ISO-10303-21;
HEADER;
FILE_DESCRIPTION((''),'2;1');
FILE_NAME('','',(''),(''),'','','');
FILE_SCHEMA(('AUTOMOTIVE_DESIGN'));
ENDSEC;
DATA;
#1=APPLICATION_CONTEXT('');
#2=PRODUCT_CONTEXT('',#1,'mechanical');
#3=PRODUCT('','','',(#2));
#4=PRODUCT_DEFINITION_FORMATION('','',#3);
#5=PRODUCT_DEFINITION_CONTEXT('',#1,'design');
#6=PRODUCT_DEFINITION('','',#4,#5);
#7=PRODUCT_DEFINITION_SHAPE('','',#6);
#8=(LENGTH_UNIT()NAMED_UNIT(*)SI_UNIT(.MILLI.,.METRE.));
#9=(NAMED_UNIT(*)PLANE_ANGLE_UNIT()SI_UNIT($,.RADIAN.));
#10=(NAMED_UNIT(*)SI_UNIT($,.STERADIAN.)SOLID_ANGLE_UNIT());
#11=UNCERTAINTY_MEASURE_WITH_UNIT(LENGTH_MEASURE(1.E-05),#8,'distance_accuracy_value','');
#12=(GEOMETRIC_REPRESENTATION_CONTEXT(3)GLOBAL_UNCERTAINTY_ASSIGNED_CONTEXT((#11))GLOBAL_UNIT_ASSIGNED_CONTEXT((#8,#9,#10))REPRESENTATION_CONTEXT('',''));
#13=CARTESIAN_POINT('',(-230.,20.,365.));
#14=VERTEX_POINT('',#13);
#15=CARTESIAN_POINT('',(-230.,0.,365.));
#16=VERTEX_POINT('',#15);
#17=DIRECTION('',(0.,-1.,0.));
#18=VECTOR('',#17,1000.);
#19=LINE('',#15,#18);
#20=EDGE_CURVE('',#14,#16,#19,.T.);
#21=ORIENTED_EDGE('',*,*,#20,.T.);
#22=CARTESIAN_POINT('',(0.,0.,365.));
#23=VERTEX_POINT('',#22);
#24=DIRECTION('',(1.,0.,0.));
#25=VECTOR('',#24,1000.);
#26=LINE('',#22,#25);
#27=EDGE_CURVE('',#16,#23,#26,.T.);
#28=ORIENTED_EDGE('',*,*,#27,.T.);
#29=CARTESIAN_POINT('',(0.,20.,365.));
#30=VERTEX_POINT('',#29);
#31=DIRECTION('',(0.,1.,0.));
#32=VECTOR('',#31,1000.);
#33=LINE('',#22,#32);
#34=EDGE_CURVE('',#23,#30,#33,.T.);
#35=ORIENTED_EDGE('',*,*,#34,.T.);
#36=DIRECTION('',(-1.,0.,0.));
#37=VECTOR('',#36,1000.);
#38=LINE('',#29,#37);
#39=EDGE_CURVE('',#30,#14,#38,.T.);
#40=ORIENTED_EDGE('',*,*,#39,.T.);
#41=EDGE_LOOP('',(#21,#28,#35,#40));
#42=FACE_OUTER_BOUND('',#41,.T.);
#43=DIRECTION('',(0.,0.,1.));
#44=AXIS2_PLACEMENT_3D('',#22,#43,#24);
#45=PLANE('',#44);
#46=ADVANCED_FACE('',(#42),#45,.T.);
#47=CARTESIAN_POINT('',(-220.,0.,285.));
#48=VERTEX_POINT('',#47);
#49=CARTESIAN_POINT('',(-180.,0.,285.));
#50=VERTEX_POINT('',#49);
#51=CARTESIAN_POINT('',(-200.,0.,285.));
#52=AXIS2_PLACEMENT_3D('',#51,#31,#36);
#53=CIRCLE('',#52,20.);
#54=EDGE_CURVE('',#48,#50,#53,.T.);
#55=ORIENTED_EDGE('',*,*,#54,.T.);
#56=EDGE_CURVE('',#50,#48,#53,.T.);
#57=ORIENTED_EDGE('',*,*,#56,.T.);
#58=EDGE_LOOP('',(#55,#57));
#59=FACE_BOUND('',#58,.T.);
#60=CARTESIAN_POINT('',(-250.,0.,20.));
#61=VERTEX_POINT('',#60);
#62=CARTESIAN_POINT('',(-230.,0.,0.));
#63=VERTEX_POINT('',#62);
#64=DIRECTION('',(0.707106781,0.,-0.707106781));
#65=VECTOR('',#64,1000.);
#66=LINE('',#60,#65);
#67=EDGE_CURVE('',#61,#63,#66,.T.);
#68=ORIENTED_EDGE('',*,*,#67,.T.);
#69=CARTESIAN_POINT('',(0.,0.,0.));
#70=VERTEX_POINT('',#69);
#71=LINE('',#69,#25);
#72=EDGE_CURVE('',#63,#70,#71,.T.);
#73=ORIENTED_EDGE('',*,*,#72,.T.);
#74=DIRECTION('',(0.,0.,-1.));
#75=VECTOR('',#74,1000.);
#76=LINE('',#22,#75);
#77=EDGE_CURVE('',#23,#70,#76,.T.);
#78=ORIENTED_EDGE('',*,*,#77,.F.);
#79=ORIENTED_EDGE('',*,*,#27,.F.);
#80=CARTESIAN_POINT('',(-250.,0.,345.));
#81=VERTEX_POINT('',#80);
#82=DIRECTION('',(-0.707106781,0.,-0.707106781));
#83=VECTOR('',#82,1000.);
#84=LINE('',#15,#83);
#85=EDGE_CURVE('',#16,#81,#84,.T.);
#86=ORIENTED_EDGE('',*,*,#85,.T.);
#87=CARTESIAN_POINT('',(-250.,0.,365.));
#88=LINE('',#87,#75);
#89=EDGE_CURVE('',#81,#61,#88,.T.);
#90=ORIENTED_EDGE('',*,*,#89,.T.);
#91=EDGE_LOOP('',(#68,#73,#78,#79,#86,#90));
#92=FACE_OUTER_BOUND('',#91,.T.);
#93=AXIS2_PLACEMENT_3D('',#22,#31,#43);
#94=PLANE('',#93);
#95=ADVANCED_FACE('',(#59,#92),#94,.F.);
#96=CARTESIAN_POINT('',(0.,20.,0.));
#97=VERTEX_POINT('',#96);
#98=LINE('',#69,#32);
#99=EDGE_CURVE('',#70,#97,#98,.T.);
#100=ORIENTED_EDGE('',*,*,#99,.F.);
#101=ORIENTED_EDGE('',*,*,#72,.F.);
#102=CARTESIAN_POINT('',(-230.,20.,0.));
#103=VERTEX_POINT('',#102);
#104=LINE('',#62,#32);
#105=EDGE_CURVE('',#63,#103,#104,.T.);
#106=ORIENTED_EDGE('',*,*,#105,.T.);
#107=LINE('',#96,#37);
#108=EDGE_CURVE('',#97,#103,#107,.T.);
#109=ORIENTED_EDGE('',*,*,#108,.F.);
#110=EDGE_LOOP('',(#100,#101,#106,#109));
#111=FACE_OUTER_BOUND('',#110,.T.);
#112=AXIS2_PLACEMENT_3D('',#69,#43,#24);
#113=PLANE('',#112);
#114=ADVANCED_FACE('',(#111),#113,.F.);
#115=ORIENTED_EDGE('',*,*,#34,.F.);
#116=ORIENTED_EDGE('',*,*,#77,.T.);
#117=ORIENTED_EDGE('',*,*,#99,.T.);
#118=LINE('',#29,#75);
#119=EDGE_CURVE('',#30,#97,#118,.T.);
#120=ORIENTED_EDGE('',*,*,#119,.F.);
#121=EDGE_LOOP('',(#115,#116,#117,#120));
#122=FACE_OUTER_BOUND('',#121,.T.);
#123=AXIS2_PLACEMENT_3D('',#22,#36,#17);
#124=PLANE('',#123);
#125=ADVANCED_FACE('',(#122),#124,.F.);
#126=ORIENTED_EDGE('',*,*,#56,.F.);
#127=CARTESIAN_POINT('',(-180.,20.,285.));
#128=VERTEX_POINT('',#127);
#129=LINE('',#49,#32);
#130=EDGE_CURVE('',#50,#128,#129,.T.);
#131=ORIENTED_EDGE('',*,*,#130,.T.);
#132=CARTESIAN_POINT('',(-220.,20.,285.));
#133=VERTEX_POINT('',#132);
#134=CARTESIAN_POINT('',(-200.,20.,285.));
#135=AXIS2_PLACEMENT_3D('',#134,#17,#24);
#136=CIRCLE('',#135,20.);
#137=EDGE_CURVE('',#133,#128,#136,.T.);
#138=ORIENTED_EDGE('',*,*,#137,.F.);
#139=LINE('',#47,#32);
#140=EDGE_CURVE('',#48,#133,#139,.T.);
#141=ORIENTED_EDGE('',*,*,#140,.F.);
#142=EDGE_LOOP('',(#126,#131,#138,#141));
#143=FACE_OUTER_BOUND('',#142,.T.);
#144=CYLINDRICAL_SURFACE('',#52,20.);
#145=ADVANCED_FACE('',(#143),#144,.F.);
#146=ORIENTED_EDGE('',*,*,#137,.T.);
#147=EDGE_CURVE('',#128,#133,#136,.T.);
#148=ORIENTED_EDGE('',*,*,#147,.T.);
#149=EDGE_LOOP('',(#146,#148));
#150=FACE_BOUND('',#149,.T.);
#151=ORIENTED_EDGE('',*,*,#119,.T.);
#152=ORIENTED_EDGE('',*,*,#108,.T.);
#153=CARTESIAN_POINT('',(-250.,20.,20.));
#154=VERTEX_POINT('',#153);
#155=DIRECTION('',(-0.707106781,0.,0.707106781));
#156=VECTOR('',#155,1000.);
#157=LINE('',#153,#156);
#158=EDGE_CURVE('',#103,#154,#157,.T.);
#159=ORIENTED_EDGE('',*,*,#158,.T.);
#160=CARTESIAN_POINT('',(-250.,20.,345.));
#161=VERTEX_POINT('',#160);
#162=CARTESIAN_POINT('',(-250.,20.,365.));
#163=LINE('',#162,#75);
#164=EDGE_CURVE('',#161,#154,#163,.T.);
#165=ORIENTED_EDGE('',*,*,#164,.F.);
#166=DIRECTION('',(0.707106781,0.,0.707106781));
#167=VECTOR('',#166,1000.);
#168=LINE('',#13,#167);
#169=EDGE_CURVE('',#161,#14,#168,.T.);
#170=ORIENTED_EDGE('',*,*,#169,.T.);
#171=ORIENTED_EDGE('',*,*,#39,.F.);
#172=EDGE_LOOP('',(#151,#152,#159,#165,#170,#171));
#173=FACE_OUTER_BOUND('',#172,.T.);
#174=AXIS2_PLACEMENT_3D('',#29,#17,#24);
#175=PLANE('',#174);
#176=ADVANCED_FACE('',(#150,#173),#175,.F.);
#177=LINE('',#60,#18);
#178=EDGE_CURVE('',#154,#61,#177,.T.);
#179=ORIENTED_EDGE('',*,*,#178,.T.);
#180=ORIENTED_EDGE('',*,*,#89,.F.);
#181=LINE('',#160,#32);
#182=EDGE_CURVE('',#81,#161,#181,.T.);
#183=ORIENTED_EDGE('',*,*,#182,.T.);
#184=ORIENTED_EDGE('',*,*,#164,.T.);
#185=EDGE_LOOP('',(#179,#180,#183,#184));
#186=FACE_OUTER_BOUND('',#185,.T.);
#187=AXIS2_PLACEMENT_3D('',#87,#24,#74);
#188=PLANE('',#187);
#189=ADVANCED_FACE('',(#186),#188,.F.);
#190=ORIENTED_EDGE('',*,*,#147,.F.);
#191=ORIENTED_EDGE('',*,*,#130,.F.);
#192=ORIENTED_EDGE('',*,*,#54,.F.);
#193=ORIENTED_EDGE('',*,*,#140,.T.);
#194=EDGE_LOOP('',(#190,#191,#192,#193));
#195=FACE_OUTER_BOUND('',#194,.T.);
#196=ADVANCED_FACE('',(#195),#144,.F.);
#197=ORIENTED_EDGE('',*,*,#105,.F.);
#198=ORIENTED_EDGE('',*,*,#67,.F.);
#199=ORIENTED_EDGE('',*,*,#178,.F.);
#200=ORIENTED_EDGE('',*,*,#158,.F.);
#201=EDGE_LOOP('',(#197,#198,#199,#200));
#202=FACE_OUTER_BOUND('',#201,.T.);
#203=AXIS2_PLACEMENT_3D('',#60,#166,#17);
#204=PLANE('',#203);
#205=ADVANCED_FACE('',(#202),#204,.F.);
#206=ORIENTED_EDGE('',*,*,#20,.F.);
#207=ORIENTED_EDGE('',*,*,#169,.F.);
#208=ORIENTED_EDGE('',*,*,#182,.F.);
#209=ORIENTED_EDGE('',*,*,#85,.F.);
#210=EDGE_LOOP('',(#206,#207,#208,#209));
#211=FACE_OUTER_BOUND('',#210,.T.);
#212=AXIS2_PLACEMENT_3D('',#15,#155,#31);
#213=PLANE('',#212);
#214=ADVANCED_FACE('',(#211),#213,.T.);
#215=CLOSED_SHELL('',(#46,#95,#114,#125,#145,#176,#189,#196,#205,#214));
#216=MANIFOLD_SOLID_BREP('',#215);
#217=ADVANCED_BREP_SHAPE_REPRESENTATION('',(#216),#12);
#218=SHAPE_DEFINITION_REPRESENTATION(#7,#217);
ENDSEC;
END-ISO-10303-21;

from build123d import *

# Parameters (mm, degrees)
SKETCH1_W               = 250
SKETCH1_H               = 20
BOSS_EXTRUDE1_DEPTH     = 365
CHAMFER1_SIZE           = 20
CUT_EXTRUDE1_DEPTH      = 443.860023032
CUT_EXTRUDE1_DEPTH_BACK = 443.860023032
SKETCH2_R               = 20
CHAMFER2_SIZE           = 20


with BuildPart() as part:
    # Sketch1 → Boss-Extrude1 (new body)
    with BuildSketch(Plane.XY):
        with Locations((-125, 10)):
            Rectangle(SKETCH1_W, SKETCH1_H)
    extrude(amount=BOSS_EXTRUDE1_DEPTH)

    # Chamfer1
    chamfer1_edges = [part.edges().sort_by_distance(p)[0] for p in [
        (-250, 10, 365),
    ]]
    chamfer(chamfer1_edges, length=CHAMFER1_SIZE)

    # Sketch2 → Cut-Extrude1 (cut, two sides: drawn at the far end of the back side and taken through both)
    with BuildSketch(Plane(origin=(0, 20, 0), x_dir=(1, 0, 0), z_dir=(0, 1, 0)).offset(-CUT_EXTRUDE1_DEPTH_BACK)):
        with Locations(Location((-200, -285, 0), (0, 0, 180))):
            Circle(SKETCH2_R)
    extrude(amount=CUT_EXTRUDE1_DEPTH + CUT_EXTRUDE1_DEPTH_BACK, mode=Mode.SUBTRACT)

    # Chamfer2
    chamfer2_edges = [part.edges().sort_by_distance(p)[0] for p in [
        (-250, 10, 0),
    ]]
    chamfer(chamfer2_edges, length=CHAMFER2_SIZE)


solid = part.part
